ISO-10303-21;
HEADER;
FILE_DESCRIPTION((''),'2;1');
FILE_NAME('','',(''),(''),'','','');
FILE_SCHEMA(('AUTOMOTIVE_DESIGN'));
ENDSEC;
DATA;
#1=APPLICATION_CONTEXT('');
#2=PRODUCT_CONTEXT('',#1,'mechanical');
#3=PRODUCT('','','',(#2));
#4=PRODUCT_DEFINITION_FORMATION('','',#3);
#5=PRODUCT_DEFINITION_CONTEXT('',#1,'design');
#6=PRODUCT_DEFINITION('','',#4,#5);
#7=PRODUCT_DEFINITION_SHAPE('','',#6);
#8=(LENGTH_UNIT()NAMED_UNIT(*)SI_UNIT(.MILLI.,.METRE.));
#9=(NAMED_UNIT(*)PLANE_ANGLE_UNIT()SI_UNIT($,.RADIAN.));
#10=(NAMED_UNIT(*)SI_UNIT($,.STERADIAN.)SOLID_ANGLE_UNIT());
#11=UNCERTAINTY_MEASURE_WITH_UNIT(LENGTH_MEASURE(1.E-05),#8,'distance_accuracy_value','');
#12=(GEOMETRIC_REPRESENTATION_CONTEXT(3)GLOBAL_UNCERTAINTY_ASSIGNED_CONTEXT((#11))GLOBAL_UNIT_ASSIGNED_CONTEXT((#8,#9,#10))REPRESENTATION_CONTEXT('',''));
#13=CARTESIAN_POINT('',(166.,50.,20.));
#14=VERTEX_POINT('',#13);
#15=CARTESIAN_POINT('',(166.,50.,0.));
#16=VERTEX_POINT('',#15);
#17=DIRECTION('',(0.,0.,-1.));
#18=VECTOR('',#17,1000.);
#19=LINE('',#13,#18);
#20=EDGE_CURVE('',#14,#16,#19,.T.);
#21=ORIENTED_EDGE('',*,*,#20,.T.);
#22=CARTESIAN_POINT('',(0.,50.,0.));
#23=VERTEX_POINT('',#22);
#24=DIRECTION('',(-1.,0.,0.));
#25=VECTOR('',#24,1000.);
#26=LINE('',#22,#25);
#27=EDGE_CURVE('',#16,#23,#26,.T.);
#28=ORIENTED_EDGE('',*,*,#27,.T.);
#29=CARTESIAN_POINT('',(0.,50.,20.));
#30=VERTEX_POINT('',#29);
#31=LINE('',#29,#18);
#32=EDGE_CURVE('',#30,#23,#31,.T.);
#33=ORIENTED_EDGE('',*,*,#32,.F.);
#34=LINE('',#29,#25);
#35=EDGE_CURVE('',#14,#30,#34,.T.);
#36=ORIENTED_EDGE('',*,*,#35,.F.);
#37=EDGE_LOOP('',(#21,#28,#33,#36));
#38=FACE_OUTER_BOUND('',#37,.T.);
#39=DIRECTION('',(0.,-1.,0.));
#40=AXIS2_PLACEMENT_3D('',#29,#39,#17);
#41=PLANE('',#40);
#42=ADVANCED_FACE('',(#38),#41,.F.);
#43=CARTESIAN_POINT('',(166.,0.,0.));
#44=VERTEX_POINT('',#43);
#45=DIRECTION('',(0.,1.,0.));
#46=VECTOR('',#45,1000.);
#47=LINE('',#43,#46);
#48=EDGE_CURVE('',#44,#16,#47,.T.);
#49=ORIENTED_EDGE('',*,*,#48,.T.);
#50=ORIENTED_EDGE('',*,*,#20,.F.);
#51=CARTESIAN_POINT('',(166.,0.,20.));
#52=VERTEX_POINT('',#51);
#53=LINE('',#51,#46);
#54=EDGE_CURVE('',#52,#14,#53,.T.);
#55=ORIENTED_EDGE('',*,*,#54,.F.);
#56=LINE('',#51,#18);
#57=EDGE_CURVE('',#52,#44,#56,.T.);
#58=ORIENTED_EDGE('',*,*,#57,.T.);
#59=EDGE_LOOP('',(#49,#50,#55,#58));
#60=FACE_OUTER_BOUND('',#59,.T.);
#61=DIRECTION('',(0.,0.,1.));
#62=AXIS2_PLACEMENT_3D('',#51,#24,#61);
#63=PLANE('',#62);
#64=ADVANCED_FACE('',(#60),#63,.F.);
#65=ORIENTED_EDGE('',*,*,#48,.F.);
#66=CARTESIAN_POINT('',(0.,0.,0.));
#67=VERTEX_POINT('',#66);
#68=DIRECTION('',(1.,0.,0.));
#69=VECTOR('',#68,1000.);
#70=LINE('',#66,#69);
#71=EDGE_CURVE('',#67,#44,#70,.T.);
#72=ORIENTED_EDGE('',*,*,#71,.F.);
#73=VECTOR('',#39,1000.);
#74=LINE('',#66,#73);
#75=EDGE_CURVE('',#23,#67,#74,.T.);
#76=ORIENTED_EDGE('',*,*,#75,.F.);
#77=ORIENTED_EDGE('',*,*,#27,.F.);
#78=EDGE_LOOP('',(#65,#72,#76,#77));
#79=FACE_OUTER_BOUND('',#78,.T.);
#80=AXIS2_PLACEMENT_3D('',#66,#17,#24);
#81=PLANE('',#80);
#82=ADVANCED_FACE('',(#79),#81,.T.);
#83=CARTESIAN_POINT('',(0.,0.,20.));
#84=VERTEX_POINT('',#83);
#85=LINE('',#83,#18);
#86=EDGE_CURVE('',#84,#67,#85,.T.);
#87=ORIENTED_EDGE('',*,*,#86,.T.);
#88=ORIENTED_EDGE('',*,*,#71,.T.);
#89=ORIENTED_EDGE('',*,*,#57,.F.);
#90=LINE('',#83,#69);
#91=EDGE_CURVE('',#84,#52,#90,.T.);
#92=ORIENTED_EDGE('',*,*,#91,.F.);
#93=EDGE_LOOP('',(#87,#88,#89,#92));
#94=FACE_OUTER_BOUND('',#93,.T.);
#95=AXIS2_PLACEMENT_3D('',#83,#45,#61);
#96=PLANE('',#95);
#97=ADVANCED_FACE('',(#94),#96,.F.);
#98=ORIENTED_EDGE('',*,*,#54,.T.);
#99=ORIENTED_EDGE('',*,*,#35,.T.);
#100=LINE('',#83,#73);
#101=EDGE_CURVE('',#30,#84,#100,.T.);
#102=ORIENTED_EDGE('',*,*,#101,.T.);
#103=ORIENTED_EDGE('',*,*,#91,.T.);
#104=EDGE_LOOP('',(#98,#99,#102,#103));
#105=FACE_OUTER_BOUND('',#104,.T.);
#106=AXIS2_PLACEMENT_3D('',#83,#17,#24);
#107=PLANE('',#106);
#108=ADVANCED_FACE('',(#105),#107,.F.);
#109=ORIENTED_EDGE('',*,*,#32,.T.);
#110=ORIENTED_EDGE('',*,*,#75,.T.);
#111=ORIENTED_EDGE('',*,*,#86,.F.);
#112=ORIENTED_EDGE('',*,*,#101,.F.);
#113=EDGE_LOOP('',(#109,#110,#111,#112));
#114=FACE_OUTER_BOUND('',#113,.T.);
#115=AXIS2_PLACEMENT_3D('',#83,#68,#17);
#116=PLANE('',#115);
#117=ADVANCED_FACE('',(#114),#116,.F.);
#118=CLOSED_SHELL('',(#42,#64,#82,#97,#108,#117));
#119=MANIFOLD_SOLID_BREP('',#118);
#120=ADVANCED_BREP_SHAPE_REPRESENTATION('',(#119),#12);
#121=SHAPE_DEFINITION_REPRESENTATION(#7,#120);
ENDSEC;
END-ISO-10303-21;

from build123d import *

# Parameters (mm, degrees)
SKETCH1_W           = 166
SKETCH1_H           = 50
BOSS_EXTRUDE1_DEPTH = 20


with BuildPart() as part:
    # Sketch1 → Boss-Extrude1 (new body)
    with BuildSketch(Plane.XY):
        with Locations((83, 25)):
            Rectangle(SKETCH1_W, SKETCH1_H)
    extrude(amount=BOSS_EXTRUDE1_DEPTH)


solid = part.part
